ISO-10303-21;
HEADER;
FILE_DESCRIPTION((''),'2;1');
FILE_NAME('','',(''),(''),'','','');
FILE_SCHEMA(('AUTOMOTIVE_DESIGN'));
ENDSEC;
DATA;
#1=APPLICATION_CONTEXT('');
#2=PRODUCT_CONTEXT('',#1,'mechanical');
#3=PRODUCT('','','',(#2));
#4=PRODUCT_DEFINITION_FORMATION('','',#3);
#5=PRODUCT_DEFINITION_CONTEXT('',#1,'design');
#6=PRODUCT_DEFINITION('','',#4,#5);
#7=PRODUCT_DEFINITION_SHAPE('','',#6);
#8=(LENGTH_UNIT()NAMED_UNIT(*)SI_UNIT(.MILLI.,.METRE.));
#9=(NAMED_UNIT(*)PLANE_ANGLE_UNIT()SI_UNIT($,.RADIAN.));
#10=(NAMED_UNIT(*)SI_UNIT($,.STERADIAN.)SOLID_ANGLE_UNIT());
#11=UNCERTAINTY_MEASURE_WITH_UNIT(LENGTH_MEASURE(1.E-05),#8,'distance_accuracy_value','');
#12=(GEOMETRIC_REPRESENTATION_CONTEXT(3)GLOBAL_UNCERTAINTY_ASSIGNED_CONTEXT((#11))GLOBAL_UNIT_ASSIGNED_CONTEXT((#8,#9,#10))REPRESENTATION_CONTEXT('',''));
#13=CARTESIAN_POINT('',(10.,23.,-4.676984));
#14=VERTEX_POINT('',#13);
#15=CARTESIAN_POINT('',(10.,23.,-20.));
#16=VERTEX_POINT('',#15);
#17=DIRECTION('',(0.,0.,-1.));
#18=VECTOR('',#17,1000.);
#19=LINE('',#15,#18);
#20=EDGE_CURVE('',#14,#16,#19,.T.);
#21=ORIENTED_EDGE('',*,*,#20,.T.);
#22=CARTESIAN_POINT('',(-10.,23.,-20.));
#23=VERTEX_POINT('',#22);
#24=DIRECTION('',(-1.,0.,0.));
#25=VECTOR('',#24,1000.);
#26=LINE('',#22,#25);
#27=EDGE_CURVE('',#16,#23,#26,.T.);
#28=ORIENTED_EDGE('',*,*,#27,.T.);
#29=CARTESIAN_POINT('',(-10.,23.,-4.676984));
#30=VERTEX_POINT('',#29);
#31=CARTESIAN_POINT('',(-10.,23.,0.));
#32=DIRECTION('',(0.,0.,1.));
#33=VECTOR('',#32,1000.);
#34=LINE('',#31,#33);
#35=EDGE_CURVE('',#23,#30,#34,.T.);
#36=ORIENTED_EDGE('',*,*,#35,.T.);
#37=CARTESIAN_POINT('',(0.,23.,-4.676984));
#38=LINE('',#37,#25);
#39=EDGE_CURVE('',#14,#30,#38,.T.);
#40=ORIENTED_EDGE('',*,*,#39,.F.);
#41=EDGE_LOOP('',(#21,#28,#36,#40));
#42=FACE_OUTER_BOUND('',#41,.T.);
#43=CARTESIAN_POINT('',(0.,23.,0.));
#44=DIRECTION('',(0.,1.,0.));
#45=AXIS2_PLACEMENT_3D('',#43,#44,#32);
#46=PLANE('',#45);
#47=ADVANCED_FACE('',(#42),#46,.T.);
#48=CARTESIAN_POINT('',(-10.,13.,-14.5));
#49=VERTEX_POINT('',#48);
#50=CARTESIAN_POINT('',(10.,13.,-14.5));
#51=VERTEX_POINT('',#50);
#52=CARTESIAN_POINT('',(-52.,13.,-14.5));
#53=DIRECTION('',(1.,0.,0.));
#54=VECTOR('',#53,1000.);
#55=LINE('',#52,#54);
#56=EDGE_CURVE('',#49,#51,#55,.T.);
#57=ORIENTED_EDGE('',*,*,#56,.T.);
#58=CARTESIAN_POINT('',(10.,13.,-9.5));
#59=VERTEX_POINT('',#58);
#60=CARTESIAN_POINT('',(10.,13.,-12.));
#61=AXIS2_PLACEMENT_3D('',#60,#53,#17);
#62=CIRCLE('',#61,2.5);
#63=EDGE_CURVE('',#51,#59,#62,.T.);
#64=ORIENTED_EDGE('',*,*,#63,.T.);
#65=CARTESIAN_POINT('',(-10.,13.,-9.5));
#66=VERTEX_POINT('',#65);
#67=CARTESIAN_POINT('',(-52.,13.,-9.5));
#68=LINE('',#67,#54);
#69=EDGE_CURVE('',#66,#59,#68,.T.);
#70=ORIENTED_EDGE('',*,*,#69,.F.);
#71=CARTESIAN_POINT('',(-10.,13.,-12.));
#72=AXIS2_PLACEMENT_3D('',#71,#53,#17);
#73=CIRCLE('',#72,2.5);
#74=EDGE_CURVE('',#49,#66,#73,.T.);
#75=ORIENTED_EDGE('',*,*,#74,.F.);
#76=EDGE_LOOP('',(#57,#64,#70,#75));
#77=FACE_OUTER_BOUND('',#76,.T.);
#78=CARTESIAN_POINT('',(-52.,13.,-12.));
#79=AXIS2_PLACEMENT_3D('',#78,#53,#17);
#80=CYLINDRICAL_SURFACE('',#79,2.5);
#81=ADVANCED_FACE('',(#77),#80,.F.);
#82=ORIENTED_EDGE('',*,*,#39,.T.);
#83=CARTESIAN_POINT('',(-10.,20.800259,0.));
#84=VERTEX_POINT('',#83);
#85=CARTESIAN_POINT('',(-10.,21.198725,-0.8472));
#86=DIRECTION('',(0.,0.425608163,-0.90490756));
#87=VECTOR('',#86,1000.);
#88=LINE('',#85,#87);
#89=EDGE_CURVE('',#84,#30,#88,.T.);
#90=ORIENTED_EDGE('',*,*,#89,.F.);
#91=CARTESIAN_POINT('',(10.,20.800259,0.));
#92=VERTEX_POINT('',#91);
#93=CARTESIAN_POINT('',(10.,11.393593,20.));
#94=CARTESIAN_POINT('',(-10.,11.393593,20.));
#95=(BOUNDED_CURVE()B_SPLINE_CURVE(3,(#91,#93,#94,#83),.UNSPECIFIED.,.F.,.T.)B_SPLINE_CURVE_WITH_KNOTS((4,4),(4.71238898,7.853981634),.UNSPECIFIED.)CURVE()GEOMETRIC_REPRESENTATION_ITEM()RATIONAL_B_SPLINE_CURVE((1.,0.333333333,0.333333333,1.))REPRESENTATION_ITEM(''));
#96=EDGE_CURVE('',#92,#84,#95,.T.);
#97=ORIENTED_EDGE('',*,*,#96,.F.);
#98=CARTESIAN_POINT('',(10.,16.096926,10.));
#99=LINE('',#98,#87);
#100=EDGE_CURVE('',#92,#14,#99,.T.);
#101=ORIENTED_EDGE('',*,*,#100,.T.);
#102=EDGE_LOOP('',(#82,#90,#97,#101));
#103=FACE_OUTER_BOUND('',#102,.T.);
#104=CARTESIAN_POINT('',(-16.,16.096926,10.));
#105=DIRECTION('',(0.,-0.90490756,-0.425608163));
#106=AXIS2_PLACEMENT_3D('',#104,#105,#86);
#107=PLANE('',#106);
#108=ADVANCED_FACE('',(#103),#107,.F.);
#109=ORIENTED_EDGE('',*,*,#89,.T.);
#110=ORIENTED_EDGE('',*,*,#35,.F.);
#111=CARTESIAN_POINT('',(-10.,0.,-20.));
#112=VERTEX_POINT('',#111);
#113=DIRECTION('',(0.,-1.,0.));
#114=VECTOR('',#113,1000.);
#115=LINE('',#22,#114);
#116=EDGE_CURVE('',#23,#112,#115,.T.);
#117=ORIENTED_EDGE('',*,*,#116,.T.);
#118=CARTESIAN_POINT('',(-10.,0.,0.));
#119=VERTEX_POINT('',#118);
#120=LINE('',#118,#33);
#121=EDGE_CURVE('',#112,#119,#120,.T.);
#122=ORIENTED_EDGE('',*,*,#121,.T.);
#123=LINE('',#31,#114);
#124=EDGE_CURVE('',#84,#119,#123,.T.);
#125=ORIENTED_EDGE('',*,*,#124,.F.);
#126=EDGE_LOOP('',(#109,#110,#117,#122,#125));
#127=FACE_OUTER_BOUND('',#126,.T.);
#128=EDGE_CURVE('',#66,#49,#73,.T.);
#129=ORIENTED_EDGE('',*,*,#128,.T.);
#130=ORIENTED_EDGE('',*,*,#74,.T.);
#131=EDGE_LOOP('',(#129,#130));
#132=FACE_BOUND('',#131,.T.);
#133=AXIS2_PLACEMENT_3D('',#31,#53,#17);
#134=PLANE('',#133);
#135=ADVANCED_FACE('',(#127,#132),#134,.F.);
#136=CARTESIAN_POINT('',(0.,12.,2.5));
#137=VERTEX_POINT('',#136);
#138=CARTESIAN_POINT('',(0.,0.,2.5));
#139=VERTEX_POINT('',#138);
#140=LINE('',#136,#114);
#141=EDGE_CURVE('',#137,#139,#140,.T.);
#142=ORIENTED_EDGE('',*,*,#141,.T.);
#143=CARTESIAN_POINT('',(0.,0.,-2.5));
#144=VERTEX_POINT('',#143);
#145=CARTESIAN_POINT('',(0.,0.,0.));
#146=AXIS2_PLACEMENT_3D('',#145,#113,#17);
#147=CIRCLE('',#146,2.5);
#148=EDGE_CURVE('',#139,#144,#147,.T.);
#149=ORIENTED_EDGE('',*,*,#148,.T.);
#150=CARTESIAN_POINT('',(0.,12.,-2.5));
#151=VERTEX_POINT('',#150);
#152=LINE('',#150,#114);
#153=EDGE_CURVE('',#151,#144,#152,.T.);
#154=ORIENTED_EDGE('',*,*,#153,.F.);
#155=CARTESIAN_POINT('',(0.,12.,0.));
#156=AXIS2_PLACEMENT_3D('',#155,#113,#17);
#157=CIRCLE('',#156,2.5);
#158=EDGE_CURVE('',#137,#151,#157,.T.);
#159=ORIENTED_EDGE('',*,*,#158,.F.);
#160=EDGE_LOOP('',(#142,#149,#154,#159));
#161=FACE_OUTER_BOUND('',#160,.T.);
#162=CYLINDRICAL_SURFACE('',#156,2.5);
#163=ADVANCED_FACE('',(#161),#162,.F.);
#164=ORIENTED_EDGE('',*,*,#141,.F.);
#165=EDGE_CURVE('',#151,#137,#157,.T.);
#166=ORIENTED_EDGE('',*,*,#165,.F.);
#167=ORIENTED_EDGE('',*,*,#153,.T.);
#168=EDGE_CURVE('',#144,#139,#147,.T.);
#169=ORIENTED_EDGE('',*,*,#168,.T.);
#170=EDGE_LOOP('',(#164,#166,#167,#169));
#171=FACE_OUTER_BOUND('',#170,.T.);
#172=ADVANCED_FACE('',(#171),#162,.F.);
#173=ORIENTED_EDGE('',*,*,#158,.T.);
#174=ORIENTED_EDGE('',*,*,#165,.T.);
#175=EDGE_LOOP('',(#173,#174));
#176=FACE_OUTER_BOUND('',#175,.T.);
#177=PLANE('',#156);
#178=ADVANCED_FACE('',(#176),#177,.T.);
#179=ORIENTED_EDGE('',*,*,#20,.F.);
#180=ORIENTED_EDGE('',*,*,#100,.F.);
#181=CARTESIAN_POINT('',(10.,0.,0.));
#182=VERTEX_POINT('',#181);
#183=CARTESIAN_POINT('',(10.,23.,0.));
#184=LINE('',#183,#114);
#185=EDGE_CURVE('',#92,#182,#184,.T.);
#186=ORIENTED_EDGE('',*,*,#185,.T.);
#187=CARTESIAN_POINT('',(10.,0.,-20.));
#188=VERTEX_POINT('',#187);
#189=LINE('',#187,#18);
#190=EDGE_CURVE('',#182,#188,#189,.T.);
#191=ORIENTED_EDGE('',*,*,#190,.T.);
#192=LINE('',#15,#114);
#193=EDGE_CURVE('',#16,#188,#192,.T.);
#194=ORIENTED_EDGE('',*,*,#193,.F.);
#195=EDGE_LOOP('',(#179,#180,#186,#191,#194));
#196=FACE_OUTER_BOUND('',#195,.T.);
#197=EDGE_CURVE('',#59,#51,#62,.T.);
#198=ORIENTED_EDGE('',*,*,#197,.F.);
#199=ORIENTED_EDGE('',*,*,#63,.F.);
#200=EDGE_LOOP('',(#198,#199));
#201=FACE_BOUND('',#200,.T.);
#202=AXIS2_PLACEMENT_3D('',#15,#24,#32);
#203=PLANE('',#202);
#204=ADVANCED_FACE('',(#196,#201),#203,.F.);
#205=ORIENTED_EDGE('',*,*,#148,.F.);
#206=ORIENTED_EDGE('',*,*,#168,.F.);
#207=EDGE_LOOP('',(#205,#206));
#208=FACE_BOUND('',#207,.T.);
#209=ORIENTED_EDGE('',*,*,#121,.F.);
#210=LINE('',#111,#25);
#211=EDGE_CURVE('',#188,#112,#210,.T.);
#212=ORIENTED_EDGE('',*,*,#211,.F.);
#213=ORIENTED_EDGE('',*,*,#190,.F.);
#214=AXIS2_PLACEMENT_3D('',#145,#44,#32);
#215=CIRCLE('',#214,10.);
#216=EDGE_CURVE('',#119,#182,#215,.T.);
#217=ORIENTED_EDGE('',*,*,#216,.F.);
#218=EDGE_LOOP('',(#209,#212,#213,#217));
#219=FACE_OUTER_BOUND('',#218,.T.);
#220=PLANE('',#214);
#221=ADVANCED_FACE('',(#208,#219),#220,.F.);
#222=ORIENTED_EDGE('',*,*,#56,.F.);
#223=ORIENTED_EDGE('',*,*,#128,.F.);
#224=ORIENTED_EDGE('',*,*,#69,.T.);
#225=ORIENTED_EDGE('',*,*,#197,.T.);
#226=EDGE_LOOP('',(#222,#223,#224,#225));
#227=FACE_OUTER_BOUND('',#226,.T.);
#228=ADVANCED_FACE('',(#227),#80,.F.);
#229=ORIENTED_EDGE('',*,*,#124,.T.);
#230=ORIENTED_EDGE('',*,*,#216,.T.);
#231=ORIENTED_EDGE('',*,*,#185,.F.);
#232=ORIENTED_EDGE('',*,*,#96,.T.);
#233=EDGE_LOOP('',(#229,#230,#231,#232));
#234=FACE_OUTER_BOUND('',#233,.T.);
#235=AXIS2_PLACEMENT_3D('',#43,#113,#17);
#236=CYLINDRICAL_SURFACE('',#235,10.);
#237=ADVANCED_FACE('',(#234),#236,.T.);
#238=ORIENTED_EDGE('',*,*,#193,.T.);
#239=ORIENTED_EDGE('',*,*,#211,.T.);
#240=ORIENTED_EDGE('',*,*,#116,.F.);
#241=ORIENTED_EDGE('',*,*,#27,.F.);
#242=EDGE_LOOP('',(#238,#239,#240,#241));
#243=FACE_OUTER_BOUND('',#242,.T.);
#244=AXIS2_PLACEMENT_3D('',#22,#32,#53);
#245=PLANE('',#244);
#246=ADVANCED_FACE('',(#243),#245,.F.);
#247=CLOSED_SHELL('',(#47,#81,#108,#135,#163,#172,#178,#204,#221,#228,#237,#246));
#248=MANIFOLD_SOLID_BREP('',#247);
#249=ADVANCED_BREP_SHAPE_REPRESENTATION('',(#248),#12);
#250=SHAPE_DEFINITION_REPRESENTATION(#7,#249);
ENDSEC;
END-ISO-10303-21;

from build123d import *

# Parameters (mm, degrees)
EXTRUDE_1_DEPTH     = 23
SKETCH_2_R          = 2.5
CUT_EXTRUDE_1_DEPTH = 12
SKETCH_3_R          = 2.5
CUT_EXTRUDE_2_DEPTH = 62
CUT_EXTRUDE_3_DEPTH = 26


with BuildPart() as part:
    # 草图1 → 凸台-拉伸1 (new body)
    with BuildSketch(Plane(origin=(0, 0, 0), x_dir=(1, 0, 0), z_dir=(0, 1, 0))):
        with BuildLine():
            Line((-10, 0), (-10, 20))
            Line((-10, 20), (10, 20))
            Line((10, 20), (10, 0))
            ThreePointArc((10, 0), (0, -10), (-10, 0))
        make_face()
    extrude(amount=EXTRUDE_1_DEPTH)

    # 草图2 → 切除-拉伸1 (cut)
    with BuildSketch(Plane.XZ):
        with Locations(Location((0, 0, 0), (0, 0, 270))):
            Circle(SKETCH_2_R)
    extrude(amount=-CUT_EXTRUDE_1_DEPTH, mode=Mode.SUBTRACT)

    # 草图3 → 切除-拉伸2 (cut)
    with BuildSketch(Plane(origin=(10, 0, 0), x_dir=(0, 0, -1), z_dir=(1, 0, 0))):
        with Locations((12, 13)):
            Circle(SKETCH_3_R)
    extrude(amount=-CUT_EXTRUDE_2_DEPTH, mode=Mode.SUBTRACT)

    # 草图4 → 切除-拉伸3 (cut)
    with BuildSketch(Plane(origin=(10, 0, 0), x_dir=(0, 0, -1), z_dir=(1, 0, 0))):
        Polygon((0, 23), (-10, 23), (-10, 16.096925585), (4.676984075, 23), align=None)
    extrude(amount=-CUT_EXTRUDE_3_DEPTH, mode=Mode.SUBTRACT)


solid = part.part
